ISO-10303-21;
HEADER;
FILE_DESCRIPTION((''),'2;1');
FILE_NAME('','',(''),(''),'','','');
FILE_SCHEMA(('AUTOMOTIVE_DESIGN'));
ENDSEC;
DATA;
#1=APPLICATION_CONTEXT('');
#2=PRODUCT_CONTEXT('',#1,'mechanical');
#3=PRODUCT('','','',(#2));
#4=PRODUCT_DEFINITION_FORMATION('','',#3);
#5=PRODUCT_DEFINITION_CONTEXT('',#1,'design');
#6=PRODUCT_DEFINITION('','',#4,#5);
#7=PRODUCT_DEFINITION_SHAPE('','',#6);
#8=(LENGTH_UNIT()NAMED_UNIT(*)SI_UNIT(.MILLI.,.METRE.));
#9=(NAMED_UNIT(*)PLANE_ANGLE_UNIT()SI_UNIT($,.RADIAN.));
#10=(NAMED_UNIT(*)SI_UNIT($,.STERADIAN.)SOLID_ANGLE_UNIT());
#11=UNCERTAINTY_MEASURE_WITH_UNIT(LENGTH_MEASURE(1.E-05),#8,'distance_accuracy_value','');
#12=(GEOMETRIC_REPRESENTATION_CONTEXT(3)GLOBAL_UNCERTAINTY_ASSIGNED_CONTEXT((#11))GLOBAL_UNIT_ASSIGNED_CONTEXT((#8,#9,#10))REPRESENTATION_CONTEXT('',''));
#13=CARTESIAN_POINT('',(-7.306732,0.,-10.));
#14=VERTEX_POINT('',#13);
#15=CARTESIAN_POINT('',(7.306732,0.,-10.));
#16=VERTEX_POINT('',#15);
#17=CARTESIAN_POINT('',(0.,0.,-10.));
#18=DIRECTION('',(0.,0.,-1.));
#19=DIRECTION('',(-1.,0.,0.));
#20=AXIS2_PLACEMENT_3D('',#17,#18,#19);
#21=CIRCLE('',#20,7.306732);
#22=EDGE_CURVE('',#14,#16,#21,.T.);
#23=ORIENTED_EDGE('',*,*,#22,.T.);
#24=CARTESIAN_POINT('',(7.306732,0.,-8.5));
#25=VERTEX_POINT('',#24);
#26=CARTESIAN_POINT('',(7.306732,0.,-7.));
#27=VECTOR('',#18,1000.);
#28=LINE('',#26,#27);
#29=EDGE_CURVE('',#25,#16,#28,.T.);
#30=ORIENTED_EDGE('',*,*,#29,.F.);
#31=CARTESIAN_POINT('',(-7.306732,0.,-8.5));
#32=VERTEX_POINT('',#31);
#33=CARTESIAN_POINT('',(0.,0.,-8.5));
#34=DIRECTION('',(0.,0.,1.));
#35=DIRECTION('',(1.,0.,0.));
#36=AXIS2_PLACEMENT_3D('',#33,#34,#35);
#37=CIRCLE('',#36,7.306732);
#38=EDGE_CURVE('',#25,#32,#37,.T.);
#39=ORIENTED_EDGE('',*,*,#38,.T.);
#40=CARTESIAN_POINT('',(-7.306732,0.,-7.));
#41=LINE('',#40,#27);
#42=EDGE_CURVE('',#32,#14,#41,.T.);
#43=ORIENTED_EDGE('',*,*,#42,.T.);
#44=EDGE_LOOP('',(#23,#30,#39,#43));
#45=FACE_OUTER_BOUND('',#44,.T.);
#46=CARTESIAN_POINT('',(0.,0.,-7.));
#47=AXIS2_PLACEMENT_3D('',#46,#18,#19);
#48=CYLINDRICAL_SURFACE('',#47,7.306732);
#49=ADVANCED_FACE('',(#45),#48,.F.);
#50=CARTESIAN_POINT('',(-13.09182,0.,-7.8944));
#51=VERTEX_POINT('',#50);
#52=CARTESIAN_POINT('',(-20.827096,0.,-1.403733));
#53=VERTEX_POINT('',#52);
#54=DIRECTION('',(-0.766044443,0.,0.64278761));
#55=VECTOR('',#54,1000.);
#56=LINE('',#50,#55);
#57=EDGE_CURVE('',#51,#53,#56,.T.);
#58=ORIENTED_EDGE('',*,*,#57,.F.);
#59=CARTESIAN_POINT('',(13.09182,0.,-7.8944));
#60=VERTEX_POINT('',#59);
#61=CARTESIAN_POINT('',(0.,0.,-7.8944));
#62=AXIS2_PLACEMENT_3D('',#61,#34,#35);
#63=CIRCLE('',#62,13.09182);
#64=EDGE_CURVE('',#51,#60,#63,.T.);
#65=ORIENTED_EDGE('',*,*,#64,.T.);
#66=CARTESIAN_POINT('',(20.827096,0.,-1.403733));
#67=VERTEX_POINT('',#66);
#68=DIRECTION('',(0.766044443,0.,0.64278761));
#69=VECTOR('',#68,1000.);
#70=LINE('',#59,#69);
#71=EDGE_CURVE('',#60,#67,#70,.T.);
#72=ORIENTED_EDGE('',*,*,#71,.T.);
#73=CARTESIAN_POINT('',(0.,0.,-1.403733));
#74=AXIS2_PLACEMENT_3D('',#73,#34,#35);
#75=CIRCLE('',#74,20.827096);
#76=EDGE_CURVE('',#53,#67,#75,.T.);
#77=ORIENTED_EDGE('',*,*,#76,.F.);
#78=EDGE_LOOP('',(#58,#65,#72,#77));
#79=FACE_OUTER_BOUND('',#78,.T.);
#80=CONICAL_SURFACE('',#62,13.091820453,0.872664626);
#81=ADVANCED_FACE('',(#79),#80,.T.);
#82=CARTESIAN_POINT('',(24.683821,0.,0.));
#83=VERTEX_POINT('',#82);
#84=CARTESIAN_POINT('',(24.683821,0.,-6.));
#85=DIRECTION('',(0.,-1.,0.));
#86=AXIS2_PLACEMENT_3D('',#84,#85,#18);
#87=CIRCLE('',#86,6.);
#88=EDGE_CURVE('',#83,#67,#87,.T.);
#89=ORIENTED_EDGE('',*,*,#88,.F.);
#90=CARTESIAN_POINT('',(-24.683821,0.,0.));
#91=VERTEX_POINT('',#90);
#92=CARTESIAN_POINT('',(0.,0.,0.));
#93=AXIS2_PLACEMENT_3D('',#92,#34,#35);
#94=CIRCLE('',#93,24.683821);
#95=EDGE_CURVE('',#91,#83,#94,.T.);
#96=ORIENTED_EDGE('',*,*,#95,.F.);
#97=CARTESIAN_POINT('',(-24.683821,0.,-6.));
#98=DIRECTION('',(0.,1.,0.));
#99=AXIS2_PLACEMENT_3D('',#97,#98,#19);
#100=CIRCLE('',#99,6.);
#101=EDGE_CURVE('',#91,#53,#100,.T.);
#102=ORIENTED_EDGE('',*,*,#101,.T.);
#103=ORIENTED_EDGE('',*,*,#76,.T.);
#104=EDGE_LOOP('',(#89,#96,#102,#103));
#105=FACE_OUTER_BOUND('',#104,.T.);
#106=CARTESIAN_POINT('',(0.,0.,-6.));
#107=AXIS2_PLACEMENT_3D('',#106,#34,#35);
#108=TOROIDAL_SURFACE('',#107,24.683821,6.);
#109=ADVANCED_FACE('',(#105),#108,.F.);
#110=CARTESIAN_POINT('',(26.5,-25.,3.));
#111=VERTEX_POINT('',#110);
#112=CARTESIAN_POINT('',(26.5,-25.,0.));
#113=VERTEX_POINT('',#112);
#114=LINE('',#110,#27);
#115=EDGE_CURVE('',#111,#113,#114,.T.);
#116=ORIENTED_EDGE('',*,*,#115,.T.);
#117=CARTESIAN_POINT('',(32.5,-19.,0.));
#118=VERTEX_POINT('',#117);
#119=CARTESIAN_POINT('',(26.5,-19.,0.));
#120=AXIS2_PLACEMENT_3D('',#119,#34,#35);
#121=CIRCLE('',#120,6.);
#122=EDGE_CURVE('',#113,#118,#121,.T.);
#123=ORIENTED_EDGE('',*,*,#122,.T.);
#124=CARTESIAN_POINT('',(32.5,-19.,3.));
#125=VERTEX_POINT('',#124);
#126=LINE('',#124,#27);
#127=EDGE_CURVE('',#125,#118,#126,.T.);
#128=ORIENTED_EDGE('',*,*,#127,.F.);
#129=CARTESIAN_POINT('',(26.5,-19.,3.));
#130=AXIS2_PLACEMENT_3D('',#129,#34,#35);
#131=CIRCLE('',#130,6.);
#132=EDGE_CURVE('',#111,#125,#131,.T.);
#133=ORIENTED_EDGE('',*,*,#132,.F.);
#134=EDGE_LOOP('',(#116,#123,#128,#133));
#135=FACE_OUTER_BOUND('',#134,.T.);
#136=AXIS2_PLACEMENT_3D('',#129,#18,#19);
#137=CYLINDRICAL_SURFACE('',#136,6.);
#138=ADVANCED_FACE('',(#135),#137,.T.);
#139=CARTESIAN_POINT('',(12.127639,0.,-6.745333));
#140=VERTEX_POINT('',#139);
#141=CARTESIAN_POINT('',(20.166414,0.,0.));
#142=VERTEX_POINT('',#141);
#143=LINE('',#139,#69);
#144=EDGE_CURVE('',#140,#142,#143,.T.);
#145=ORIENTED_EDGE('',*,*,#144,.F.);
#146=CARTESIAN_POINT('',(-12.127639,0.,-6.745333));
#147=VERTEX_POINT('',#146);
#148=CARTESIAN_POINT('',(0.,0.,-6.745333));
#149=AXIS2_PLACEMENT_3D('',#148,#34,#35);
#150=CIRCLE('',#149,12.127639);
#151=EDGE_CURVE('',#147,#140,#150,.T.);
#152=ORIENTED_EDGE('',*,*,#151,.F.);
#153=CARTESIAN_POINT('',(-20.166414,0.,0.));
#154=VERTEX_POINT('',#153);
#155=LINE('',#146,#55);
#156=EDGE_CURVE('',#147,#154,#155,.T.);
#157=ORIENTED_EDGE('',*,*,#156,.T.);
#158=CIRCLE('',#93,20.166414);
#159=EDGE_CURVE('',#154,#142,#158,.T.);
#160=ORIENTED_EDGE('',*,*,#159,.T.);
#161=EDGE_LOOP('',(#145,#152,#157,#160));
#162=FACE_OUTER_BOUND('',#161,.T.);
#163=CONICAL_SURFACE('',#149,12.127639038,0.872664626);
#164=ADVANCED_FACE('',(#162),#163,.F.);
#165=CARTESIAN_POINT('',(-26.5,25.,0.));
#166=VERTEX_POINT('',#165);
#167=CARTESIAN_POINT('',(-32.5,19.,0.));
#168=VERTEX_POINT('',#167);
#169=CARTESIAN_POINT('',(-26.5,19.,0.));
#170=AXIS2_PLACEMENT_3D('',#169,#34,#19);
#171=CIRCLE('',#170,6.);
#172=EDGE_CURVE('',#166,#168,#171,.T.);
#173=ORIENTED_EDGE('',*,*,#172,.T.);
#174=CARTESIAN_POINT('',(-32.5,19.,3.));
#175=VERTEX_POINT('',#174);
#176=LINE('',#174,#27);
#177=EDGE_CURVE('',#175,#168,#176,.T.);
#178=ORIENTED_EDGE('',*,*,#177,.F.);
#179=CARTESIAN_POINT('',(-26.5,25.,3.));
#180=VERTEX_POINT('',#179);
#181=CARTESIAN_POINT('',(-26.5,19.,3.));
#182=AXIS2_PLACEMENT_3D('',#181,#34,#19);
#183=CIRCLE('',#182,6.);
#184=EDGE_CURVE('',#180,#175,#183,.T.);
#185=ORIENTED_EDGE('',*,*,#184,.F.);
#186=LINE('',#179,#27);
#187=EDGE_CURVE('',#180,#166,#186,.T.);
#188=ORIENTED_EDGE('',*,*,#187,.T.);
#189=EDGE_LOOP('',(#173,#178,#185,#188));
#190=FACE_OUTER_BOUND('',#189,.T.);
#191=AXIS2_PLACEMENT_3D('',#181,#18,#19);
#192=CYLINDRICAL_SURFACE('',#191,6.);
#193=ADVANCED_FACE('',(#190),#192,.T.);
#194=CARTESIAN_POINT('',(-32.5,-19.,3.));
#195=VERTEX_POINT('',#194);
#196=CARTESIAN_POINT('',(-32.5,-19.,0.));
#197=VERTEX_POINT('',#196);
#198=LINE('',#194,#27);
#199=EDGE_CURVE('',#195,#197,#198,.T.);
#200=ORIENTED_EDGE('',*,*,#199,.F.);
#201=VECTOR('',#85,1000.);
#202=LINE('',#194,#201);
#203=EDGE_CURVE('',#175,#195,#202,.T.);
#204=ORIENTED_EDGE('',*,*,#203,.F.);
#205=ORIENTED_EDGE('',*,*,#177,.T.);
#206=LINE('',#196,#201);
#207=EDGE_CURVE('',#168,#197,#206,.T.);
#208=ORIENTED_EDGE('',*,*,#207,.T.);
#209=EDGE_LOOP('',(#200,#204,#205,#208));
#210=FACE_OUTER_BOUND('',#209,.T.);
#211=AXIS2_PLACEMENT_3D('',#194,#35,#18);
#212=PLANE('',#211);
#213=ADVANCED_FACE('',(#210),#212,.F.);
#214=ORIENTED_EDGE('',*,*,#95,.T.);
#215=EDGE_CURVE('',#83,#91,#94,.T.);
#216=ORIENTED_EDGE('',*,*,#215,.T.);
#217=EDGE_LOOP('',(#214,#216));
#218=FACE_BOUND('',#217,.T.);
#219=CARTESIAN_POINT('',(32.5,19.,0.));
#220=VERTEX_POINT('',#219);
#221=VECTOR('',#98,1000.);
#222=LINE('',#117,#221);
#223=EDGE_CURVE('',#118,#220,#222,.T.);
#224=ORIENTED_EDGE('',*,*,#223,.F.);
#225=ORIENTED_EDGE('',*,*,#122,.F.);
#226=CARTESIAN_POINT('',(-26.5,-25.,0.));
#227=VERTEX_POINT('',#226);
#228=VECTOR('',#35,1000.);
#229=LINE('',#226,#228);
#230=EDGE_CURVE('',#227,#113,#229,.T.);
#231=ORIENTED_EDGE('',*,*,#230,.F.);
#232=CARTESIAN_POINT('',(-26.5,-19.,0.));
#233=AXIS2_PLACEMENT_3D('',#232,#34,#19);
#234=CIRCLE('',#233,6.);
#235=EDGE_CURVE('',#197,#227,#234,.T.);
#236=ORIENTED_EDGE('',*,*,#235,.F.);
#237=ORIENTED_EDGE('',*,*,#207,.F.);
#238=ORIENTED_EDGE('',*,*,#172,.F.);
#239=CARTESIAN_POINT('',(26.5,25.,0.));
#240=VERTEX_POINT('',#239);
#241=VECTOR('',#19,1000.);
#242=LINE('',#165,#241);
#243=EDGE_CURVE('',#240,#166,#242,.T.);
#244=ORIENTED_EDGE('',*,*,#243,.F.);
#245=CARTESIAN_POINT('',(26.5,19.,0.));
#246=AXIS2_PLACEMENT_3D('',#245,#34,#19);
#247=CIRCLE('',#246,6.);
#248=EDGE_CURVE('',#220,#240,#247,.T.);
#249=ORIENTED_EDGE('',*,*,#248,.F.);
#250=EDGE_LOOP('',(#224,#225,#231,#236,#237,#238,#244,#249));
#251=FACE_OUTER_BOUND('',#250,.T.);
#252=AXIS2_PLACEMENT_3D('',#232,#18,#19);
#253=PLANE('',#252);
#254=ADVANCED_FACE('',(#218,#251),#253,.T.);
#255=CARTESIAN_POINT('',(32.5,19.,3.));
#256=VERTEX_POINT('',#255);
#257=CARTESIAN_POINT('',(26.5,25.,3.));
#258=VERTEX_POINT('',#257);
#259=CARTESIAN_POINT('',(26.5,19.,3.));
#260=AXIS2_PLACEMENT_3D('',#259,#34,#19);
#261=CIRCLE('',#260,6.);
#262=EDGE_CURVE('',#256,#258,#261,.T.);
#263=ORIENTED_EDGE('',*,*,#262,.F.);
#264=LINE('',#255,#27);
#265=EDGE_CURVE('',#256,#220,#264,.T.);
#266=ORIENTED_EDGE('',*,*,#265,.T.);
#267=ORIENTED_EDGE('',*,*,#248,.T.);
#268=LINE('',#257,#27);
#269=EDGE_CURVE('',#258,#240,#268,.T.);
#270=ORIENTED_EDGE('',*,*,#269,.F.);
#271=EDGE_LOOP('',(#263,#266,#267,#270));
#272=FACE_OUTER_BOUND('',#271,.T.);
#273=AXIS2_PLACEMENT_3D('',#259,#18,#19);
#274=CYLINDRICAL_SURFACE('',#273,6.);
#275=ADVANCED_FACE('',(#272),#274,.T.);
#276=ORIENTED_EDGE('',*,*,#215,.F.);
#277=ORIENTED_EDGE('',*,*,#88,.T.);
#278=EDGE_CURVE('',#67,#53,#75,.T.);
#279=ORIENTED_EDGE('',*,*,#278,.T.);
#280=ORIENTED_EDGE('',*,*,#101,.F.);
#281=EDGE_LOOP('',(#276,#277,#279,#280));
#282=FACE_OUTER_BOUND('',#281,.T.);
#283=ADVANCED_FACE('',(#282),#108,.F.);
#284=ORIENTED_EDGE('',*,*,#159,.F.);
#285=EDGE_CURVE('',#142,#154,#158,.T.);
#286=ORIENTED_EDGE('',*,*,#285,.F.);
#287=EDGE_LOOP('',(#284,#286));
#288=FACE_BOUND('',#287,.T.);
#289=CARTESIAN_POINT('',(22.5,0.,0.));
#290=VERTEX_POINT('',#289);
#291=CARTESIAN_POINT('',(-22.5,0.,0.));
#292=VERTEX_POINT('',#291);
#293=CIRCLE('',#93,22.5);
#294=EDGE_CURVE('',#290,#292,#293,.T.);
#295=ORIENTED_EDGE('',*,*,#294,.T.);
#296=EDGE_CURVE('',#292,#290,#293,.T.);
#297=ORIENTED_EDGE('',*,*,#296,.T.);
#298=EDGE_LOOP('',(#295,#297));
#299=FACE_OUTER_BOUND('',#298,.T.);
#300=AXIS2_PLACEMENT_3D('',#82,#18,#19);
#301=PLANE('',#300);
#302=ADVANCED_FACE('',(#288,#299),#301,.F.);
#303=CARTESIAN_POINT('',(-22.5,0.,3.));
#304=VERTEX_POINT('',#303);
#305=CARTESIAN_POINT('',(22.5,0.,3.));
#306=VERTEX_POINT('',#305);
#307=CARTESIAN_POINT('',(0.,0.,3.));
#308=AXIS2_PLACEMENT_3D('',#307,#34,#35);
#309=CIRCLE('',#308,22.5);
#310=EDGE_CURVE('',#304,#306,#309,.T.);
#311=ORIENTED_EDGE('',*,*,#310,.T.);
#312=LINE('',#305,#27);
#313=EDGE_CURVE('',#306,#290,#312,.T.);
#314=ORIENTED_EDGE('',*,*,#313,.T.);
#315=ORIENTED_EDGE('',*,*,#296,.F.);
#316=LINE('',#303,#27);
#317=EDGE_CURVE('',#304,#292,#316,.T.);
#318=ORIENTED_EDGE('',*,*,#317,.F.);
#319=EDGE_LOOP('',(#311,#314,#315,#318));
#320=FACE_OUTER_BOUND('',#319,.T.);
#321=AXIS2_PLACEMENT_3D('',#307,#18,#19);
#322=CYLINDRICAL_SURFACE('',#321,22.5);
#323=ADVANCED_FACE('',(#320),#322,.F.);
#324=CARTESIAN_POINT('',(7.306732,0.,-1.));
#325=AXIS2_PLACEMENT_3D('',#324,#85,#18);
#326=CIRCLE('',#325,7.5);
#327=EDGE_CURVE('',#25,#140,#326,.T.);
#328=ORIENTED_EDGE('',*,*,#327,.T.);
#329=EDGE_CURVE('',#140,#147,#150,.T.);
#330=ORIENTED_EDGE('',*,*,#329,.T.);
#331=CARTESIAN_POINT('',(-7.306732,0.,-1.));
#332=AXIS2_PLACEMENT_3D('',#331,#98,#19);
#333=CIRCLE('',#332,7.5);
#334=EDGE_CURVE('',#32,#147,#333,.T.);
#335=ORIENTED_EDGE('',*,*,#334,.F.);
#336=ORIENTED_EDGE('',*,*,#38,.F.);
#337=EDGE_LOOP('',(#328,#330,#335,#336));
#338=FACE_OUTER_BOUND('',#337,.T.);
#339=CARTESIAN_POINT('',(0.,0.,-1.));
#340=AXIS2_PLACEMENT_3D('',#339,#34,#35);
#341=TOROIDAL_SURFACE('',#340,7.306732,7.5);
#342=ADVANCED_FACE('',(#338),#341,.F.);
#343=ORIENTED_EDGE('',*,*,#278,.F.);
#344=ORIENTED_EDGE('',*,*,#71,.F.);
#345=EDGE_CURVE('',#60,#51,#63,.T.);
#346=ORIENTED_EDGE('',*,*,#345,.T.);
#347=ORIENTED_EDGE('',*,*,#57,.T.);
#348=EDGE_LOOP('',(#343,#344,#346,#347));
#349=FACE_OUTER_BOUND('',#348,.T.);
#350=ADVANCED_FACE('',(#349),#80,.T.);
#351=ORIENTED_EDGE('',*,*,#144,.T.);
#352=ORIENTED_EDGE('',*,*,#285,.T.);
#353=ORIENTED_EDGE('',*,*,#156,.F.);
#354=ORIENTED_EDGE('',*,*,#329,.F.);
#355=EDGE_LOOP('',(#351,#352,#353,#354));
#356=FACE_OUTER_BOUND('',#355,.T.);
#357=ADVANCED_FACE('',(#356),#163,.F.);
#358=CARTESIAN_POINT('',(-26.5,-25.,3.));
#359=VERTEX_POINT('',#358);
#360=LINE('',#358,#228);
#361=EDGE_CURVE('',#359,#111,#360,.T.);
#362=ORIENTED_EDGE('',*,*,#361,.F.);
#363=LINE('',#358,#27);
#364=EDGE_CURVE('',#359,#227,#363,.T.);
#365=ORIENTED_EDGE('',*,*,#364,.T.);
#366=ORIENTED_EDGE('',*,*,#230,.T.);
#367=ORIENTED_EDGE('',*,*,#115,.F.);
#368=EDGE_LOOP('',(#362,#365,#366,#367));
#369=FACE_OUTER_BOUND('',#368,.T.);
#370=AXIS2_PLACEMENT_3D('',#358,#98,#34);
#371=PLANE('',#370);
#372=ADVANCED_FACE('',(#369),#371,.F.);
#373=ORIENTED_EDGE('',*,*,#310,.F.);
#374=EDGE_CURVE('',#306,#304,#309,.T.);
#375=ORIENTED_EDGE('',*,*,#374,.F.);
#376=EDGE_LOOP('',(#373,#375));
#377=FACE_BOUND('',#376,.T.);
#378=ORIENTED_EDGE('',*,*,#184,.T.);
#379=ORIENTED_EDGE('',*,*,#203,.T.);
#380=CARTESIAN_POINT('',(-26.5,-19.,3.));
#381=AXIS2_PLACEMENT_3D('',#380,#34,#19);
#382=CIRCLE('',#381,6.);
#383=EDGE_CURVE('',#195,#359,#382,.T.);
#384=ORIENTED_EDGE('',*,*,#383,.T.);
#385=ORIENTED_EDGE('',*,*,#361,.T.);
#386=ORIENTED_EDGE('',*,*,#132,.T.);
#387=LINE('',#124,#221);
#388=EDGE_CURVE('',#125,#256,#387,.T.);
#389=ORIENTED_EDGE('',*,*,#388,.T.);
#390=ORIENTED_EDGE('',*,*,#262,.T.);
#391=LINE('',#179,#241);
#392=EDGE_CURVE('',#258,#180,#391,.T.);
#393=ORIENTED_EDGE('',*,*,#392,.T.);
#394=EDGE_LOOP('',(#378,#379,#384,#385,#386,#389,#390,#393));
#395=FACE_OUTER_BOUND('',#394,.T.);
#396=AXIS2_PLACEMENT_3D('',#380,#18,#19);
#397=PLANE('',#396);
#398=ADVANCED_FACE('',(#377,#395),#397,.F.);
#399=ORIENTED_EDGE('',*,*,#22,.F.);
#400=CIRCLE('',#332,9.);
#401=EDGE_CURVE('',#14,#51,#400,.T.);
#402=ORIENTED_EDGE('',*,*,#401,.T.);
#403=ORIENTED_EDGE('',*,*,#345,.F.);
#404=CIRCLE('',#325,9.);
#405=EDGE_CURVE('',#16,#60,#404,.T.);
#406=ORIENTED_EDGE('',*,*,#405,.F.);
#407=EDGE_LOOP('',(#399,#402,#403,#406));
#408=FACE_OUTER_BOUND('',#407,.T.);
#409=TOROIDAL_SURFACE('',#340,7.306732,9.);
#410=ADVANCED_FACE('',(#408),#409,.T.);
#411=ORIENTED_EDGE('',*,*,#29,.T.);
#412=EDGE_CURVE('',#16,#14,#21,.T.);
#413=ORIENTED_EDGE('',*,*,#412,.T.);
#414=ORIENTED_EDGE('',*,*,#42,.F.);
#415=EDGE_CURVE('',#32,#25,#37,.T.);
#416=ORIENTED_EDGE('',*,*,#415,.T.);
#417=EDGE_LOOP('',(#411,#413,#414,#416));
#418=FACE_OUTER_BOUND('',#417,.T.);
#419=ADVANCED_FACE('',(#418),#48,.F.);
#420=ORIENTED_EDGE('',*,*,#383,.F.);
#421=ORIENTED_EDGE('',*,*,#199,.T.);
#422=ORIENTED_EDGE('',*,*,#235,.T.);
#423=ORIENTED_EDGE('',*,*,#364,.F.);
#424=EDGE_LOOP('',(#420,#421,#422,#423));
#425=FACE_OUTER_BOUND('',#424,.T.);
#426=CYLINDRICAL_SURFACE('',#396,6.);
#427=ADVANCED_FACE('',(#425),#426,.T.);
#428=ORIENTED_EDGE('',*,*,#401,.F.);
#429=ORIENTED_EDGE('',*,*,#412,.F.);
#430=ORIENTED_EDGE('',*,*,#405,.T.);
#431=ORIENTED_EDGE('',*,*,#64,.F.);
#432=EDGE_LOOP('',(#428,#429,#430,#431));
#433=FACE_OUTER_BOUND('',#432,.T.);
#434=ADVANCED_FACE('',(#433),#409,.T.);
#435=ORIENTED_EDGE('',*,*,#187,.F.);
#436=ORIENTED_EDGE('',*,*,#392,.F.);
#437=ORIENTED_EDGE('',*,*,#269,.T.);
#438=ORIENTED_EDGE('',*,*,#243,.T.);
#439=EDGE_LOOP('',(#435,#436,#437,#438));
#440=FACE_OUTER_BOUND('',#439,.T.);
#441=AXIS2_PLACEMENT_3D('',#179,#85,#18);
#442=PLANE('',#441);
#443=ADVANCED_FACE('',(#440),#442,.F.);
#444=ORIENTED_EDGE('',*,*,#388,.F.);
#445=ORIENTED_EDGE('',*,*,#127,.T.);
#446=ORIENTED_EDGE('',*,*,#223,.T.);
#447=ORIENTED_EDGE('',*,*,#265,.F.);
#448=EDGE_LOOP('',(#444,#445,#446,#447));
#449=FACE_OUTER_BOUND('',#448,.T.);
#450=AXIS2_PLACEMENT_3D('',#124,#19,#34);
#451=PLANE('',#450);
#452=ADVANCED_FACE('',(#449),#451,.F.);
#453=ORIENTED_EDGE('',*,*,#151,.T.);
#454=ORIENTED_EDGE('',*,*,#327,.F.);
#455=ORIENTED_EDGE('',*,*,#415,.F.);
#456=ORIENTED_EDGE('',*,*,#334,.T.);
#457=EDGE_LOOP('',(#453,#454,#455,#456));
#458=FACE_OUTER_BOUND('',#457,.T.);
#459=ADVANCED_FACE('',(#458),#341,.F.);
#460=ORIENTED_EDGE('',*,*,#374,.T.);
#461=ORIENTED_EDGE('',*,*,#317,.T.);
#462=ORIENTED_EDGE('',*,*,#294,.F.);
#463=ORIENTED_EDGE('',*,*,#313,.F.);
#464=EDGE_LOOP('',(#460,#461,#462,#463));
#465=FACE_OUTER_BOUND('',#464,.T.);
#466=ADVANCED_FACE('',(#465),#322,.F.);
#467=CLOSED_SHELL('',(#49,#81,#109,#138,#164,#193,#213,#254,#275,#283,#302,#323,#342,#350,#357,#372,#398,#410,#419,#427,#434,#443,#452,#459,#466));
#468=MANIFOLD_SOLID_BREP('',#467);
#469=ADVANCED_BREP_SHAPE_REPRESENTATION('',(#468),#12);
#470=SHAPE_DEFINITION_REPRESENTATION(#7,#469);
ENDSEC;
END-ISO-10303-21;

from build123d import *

# Parameters (mm, degrees)
PLATE_PROFILE_SKETCH_R    = 22.5
BASE_PLATE_65X50X3_DEPTH  = 3
CENTRE_HOLE_SKETCH_R      = 7.306731966
CENTRE_THROUGH_HOLE_DEPTH = 3


with BuildPart() as part:
    # Plate Profile Sketch → Base Plate 65x50x3 (new body)
    with BuildSketch(Plane.XY):
        with BuildLine():
            Line((-26.5, -25), (26.5, -25))
            ThreePointArc((26.5, -25), (30.742640687, -23.242640687), (32.5, -19))
            Line((32.5, -19), (32.5, 19))
            ThreePointArc((32.5, 19), (30.742640687, 23.242640687), (26.5, 25))
            Line((26.5, 25), (-26.5, 25))
            ThreePointArc((-26.5, 25), (-30.742640687, 23.242640687), (-32.5, 19))
            Line((-32.5, 19), (-32.5, -19))
            ThreePointArc((-32.5, -19), (-30.742640687, -23.242640687), (-26.5, -25))
        make_face()
        Circle(PLATE_PROFILE_SKETCH_R, mode=Mode.SUBTRACT)
    extrude(amount=BASE_PLATE_65X50X3_DEPTH)

    # Conical Dimple Profile Sketch → Conical Dimple (revolve)
    with BuildSketch(Plane(origin=(0, 0, 0), x_dir=(1, 0, 0), z_dir=(0, 1, 0))):
        with BuildLine():
            Line((13.091820453, 7.894399988), (20.827095747, 1.403733341))
            ThreePointArc((20.827095747, 1.403733341), (22.631700546, 0.361844275), (24.683821406, 0))
            Line((24.683821406, 0), (20.16641426, 0))
            Line((20.16641426, 0), (12.127639038, 6.745333323))
            ThreePointArc((12.127639038, 6.745333323), (9.871883041, 8.047694656), (7.306731966, 8.5))
            Line((7.306731966, 8.5), (0, 8.5))
            Line((0, 8.5), (0, 10))
            Line((0, 10), (7.306731966, 10))
            ThreePointArc((7.306731966, 10), (10.384913256, 9.457233587), (13.091820453, 7.894399988))
        make_face()
    revolve(axis=Axis((0, 0, 5.787775716), (0, 0, -1)))

    # Centre Hole Sketch → Centre Through Hole (cut)
    with BuildSketch(Plane(origin=(0, 0, -10), x_dir=(-1, 0, 0), z_dir=(0, 0, -1))):
        with Locations(Location((0, 0, 0), (0, 0, 180))):
            Circle(CENTRE_HOLE_SKETCH_R)
    extrude(amount=-CENTRE_THROUGH_HOLE_DEPTH, mode=Mode.SUBTRACT)


solid = part.part
